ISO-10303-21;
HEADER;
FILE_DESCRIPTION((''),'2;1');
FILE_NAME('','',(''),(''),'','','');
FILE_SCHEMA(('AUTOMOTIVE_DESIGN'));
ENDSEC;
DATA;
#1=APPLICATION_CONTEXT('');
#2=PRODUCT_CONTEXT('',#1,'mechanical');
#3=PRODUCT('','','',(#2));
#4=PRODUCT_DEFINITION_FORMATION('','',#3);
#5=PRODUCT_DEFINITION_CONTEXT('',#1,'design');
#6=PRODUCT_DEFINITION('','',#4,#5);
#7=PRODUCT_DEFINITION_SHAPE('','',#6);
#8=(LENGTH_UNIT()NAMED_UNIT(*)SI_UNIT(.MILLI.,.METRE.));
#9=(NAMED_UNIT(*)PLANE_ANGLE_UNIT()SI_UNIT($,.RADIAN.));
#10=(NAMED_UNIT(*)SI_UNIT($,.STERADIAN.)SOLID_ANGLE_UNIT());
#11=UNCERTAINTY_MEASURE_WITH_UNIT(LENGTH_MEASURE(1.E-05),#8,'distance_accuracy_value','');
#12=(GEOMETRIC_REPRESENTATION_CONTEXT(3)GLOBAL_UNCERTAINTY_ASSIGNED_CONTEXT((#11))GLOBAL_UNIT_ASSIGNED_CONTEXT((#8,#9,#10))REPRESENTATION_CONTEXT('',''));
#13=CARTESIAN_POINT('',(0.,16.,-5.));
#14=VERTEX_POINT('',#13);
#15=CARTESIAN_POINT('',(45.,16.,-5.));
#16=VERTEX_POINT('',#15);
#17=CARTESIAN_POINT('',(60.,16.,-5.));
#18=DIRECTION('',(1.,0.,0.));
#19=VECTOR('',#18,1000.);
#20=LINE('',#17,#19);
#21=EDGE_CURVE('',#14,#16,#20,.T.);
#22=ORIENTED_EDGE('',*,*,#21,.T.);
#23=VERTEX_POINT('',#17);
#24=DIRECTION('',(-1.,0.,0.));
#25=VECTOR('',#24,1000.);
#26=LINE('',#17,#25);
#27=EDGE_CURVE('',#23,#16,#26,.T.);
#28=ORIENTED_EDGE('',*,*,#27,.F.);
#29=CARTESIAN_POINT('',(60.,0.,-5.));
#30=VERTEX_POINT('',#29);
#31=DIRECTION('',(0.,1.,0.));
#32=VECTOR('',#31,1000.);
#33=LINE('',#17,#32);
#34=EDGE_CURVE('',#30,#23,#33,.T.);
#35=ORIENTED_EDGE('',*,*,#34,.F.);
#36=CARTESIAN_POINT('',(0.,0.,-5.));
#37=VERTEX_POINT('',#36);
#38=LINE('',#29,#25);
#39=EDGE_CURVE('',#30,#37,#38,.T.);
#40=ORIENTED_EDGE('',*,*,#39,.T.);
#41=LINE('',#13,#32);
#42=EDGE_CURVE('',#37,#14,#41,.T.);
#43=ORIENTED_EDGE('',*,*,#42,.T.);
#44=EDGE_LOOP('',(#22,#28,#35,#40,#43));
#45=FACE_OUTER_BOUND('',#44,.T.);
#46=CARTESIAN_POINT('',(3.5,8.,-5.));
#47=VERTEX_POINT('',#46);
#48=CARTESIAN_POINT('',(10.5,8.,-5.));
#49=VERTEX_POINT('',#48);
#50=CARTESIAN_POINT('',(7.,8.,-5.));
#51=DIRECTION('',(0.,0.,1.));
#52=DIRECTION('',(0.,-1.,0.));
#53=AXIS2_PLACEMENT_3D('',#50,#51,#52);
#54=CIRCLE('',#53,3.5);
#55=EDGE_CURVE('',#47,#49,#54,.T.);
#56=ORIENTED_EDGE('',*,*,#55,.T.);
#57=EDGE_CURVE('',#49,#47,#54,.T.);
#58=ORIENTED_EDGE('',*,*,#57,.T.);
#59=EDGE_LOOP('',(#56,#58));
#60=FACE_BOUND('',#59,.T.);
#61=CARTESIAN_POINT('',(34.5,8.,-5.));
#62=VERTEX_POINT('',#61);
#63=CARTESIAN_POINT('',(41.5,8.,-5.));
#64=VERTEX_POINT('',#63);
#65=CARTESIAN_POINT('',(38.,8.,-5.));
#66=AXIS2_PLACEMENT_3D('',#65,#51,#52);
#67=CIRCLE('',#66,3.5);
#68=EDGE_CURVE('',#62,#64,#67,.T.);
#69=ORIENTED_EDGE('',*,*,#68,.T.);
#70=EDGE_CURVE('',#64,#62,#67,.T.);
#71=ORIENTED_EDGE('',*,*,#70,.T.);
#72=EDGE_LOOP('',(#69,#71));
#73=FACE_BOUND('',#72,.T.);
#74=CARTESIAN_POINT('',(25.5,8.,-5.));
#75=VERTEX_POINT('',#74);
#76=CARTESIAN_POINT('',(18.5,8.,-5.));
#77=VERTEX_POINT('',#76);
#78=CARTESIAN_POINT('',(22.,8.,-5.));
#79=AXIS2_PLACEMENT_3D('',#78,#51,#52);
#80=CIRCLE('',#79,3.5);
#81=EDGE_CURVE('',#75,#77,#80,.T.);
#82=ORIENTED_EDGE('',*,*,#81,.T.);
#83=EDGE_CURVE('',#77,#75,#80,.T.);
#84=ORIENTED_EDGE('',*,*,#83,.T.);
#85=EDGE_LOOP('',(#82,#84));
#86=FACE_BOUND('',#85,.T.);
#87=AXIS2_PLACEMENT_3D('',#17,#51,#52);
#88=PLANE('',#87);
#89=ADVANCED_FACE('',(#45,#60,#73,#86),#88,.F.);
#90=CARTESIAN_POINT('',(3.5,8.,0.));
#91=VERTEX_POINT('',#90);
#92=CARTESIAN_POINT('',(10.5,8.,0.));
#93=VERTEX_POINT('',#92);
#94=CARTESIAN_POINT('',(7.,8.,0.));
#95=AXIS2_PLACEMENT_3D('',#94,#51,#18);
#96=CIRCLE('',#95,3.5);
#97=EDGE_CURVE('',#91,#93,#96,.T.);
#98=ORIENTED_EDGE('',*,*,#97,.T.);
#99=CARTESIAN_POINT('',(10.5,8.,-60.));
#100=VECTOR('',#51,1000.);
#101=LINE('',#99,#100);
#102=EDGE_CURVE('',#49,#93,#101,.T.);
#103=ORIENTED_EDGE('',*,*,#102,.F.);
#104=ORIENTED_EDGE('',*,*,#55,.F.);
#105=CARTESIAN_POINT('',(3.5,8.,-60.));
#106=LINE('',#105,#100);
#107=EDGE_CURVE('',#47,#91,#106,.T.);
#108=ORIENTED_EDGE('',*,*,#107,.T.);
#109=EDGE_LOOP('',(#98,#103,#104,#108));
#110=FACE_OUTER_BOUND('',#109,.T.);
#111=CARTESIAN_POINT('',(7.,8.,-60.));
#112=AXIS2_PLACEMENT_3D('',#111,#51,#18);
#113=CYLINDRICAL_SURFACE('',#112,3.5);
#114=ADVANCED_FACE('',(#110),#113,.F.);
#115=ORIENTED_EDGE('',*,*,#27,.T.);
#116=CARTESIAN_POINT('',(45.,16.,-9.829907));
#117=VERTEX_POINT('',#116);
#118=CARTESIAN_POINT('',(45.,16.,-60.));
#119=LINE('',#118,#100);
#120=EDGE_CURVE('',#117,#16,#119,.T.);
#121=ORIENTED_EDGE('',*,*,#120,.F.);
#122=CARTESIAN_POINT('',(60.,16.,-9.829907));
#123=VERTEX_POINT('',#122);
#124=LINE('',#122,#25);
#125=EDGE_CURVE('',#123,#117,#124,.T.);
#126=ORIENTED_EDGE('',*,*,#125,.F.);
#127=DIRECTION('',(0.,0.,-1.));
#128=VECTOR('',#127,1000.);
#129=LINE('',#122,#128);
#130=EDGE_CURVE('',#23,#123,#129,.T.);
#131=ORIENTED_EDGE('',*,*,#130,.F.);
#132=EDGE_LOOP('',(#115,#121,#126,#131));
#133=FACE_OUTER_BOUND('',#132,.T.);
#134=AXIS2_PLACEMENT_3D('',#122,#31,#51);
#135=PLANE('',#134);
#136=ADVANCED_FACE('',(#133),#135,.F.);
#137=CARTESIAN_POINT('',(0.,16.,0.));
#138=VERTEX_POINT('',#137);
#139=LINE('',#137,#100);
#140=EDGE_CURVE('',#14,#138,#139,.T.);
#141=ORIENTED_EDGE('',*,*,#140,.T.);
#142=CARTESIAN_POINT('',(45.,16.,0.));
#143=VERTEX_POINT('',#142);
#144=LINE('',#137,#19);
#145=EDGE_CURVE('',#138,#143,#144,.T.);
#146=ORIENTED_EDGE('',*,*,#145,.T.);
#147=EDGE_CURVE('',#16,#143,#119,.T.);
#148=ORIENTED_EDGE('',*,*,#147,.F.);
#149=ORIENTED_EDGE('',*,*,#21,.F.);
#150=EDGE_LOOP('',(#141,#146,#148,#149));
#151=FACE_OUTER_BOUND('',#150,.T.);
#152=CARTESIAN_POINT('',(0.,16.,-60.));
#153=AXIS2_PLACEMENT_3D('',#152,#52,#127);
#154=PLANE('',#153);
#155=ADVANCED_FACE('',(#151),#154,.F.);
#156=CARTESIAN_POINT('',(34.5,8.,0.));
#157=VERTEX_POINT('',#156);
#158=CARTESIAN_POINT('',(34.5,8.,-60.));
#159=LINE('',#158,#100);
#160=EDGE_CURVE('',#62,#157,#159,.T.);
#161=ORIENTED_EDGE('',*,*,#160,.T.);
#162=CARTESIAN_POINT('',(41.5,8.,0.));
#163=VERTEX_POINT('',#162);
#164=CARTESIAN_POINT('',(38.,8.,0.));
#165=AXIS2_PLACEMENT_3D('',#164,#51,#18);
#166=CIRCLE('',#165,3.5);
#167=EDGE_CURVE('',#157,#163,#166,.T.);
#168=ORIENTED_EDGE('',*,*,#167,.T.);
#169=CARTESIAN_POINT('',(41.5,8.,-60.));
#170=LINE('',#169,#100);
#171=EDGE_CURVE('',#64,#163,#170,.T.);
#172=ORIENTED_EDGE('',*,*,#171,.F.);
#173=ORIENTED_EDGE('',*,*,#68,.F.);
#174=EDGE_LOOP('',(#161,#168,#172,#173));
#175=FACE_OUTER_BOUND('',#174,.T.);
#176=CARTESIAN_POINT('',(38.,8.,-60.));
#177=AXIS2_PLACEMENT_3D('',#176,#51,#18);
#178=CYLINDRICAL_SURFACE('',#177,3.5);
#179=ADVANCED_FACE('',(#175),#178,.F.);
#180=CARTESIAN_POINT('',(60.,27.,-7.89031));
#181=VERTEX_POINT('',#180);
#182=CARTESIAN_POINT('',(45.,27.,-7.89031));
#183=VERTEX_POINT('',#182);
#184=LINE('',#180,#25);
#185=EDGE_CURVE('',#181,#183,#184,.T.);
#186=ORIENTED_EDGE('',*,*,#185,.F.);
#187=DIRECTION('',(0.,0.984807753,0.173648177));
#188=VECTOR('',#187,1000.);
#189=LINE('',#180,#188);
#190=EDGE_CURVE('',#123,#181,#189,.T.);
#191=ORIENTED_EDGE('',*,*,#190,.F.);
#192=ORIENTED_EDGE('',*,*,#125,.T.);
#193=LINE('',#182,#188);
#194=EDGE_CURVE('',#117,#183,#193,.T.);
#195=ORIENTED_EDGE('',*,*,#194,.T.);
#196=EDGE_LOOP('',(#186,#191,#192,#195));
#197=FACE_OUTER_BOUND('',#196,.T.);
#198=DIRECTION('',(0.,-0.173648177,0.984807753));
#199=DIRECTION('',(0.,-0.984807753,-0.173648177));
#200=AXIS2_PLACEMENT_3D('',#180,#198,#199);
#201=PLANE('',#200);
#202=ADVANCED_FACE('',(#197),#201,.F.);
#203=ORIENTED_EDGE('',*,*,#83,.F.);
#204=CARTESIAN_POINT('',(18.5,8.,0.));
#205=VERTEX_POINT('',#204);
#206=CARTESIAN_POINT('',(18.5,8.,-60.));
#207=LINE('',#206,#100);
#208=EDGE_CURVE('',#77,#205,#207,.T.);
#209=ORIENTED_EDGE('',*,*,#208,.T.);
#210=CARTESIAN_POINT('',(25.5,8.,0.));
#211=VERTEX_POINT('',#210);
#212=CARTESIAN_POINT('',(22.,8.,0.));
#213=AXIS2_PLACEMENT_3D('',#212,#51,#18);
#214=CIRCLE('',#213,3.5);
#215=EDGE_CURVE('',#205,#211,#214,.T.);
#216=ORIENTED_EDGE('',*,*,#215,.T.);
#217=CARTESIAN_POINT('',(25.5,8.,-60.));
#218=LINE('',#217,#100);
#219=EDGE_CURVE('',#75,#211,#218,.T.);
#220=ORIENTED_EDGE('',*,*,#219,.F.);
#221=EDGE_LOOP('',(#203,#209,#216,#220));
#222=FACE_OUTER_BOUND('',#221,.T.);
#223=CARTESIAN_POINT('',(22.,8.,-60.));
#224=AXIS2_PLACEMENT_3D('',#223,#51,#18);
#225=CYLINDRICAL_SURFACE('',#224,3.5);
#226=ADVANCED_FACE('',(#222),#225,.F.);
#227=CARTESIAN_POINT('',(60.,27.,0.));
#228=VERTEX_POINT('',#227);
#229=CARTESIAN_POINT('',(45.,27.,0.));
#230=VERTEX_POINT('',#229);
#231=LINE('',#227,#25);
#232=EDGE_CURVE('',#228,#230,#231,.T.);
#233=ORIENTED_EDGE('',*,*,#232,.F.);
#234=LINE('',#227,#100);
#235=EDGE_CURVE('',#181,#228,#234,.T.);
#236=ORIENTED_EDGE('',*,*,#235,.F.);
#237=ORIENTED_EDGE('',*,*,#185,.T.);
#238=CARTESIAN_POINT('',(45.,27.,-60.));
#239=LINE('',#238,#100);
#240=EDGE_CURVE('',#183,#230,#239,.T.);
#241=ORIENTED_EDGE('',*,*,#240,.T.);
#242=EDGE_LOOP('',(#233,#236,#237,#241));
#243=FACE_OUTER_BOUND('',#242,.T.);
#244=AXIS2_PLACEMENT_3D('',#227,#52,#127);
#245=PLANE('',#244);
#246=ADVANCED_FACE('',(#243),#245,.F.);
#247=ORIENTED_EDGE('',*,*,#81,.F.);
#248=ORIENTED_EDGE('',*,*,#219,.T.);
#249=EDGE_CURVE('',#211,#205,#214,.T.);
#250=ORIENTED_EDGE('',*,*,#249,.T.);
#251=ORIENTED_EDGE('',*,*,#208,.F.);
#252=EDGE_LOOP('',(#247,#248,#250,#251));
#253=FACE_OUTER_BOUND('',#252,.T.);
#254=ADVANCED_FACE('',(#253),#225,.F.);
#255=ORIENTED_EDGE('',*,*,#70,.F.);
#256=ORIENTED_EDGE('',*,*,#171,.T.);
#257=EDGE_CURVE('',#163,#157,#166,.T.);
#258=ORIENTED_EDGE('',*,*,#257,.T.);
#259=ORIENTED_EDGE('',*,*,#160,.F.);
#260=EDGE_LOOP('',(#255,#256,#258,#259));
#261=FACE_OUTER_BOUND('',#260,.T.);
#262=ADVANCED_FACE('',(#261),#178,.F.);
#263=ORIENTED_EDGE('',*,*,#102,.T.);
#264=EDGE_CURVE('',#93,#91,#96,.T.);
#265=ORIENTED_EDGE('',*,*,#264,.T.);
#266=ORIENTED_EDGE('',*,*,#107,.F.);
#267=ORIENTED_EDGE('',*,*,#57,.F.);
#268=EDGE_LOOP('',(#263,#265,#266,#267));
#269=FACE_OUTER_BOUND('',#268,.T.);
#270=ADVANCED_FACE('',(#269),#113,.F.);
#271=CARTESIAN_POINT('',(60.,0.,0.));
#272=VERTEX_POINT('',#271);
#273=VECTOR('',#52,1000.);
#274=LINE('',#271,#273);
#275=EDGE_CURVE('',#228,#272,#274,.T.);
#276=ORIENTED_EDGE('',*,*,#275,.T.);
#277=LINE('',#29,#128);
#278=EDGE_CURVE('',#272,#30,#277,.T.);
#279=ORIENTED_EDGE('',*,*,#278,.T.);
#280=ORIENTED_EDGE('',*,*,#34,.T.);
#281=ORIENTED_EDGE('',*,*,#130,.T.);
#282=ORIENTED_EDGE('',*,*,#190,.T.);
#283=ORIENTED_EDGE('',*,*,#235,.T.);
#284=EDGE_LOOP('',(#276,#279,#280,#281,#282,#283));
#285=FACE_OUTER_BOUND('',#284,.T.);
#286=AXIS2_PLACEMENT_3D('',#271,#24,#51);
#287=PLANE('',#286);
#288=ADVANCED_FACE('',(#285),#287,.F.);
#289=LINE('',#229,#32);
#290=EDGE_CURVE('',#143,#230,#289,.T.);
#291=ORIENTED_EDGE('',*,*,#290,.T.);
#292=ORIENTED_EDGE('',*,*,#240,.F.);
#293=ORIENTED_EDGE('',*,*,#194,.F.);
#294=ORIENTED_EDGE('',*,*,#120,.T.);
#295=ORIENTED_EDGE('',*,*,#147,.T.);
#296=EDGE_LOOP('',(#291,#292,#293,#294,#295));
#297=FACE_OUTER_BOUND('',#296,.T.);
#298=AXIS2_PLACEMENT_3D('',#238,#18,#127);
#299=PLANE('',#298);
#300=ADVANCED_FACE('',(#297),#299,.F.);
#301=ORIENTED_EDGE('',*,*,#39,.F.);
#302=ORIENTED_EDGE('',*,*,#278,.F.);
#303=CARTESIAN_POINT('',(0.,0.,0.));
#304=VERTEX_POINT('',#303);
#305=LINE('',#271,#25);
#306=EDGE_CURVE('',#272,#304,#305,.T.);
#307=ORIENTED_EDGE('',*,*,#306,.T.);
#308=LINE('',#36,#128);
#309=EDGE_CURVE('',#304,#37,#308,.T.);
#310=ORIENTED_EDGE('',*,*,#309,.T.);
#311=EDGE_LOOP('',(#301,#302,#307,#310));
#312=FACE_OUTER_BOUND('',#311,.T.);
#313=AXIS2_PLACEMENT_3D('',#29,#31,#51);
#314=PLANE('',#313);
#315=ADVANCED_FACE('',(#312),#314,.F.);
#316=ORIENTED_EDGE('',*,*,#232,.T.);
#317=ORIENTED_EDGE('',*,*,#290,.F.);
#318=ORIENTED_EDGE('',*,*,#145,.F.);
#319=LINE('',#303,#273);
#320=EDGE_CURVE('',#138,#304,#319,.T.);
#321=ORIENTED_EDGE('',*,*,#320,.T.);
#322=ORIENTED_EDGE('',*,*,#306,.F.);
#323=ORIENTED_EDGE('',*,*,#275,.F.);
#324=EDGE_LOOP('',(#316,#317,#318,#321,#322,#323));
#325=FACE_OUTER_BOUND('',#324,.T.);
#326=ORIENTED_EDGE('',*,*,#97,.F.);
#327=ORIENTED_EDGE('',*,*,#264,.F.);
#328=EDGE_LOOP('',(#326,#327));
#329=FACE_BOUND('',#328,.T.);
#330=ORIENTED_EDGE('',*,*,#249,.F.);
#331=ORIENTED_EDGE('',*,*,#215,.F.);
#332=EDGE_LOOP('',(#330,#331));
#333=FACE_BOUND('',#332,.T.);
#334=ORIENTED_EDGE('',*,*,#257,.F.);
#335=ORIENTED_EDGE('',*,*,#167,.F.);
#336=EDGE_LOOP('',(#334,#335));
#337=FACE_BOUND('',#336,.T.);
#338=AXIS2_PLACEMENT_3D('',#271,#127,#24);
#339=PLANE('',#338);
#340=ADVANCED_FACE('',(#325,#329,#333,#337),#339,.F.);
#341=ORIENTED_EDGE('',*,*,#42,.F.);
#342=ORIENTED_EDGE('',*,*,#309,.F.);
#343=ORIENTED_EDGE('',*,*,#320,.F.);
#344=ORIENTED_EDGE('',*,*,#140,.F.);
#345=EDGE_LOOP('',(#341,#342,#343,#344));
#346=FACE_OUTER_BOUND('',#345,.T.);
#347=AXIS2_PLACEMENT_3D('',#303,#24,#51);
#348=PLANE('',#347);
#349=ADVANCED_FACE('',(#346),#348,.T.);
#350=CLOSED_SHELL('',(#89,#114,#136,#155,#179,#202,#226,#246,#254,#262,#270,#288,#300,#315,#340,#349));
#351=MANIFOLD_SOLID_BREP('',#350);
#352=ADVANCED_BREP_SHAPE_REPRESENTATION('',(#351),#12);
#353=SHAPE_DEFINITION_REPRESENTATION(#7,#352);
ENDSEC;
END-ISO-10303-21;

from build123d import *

# Parameters (mm, degrees)
BOSS_EXTRUDE1_DEPTH = 60
SKETCH2_W           = 45
SKETCH2_H           = 11
CUT_EXTRUDE1_DEPTH  = 60
SKETCH3_R           = 3.5
CUT_EXTRUDE2_DEPTH  = 60


with BuildPart() as part:
    # Sketch1 → Boss-Extrude1 (new body)
    with BuildSketch(Plane(origin=(0, 0, 0), x_dir=(0, 0, -1), z_dir=(1, 0, 0))):
        Polygon((0, 0), (0, 27), (7.89031, 27), (9.829906784, 16), (5, 16), (5, 0), align=None)
    extrude(amount=BOSS_EXTRUDE1_DEPTH)

    # Sketch2 → Cut-Extrude1 (cut)
    with BuildSketch(Plane.XY):
        with Locations((22.5, 21.5)):
            Rectangle(SKETCH2_W, SKETCH2_H)
    extrude(amount=-CUT_EXTRUDE1_DEPTH, mode=Mode.SUBTRACT)

    # Sketch3 → Cut-Extrude2 (cut)
    with BuildSketch(Plane.XY):
        with Locations((7, 8)):
            Circle(SKETCH3_R)
        with Locations((22, 8)):
            Circle(SKETCH3_R)
        with Locations((38, 8)):
            Circle(SKETCH3_R)
    extrude(amount=-CUT_EXTRUDE2_DEPTH, mode=Mode.SUBTRACT)


solid = part.part
